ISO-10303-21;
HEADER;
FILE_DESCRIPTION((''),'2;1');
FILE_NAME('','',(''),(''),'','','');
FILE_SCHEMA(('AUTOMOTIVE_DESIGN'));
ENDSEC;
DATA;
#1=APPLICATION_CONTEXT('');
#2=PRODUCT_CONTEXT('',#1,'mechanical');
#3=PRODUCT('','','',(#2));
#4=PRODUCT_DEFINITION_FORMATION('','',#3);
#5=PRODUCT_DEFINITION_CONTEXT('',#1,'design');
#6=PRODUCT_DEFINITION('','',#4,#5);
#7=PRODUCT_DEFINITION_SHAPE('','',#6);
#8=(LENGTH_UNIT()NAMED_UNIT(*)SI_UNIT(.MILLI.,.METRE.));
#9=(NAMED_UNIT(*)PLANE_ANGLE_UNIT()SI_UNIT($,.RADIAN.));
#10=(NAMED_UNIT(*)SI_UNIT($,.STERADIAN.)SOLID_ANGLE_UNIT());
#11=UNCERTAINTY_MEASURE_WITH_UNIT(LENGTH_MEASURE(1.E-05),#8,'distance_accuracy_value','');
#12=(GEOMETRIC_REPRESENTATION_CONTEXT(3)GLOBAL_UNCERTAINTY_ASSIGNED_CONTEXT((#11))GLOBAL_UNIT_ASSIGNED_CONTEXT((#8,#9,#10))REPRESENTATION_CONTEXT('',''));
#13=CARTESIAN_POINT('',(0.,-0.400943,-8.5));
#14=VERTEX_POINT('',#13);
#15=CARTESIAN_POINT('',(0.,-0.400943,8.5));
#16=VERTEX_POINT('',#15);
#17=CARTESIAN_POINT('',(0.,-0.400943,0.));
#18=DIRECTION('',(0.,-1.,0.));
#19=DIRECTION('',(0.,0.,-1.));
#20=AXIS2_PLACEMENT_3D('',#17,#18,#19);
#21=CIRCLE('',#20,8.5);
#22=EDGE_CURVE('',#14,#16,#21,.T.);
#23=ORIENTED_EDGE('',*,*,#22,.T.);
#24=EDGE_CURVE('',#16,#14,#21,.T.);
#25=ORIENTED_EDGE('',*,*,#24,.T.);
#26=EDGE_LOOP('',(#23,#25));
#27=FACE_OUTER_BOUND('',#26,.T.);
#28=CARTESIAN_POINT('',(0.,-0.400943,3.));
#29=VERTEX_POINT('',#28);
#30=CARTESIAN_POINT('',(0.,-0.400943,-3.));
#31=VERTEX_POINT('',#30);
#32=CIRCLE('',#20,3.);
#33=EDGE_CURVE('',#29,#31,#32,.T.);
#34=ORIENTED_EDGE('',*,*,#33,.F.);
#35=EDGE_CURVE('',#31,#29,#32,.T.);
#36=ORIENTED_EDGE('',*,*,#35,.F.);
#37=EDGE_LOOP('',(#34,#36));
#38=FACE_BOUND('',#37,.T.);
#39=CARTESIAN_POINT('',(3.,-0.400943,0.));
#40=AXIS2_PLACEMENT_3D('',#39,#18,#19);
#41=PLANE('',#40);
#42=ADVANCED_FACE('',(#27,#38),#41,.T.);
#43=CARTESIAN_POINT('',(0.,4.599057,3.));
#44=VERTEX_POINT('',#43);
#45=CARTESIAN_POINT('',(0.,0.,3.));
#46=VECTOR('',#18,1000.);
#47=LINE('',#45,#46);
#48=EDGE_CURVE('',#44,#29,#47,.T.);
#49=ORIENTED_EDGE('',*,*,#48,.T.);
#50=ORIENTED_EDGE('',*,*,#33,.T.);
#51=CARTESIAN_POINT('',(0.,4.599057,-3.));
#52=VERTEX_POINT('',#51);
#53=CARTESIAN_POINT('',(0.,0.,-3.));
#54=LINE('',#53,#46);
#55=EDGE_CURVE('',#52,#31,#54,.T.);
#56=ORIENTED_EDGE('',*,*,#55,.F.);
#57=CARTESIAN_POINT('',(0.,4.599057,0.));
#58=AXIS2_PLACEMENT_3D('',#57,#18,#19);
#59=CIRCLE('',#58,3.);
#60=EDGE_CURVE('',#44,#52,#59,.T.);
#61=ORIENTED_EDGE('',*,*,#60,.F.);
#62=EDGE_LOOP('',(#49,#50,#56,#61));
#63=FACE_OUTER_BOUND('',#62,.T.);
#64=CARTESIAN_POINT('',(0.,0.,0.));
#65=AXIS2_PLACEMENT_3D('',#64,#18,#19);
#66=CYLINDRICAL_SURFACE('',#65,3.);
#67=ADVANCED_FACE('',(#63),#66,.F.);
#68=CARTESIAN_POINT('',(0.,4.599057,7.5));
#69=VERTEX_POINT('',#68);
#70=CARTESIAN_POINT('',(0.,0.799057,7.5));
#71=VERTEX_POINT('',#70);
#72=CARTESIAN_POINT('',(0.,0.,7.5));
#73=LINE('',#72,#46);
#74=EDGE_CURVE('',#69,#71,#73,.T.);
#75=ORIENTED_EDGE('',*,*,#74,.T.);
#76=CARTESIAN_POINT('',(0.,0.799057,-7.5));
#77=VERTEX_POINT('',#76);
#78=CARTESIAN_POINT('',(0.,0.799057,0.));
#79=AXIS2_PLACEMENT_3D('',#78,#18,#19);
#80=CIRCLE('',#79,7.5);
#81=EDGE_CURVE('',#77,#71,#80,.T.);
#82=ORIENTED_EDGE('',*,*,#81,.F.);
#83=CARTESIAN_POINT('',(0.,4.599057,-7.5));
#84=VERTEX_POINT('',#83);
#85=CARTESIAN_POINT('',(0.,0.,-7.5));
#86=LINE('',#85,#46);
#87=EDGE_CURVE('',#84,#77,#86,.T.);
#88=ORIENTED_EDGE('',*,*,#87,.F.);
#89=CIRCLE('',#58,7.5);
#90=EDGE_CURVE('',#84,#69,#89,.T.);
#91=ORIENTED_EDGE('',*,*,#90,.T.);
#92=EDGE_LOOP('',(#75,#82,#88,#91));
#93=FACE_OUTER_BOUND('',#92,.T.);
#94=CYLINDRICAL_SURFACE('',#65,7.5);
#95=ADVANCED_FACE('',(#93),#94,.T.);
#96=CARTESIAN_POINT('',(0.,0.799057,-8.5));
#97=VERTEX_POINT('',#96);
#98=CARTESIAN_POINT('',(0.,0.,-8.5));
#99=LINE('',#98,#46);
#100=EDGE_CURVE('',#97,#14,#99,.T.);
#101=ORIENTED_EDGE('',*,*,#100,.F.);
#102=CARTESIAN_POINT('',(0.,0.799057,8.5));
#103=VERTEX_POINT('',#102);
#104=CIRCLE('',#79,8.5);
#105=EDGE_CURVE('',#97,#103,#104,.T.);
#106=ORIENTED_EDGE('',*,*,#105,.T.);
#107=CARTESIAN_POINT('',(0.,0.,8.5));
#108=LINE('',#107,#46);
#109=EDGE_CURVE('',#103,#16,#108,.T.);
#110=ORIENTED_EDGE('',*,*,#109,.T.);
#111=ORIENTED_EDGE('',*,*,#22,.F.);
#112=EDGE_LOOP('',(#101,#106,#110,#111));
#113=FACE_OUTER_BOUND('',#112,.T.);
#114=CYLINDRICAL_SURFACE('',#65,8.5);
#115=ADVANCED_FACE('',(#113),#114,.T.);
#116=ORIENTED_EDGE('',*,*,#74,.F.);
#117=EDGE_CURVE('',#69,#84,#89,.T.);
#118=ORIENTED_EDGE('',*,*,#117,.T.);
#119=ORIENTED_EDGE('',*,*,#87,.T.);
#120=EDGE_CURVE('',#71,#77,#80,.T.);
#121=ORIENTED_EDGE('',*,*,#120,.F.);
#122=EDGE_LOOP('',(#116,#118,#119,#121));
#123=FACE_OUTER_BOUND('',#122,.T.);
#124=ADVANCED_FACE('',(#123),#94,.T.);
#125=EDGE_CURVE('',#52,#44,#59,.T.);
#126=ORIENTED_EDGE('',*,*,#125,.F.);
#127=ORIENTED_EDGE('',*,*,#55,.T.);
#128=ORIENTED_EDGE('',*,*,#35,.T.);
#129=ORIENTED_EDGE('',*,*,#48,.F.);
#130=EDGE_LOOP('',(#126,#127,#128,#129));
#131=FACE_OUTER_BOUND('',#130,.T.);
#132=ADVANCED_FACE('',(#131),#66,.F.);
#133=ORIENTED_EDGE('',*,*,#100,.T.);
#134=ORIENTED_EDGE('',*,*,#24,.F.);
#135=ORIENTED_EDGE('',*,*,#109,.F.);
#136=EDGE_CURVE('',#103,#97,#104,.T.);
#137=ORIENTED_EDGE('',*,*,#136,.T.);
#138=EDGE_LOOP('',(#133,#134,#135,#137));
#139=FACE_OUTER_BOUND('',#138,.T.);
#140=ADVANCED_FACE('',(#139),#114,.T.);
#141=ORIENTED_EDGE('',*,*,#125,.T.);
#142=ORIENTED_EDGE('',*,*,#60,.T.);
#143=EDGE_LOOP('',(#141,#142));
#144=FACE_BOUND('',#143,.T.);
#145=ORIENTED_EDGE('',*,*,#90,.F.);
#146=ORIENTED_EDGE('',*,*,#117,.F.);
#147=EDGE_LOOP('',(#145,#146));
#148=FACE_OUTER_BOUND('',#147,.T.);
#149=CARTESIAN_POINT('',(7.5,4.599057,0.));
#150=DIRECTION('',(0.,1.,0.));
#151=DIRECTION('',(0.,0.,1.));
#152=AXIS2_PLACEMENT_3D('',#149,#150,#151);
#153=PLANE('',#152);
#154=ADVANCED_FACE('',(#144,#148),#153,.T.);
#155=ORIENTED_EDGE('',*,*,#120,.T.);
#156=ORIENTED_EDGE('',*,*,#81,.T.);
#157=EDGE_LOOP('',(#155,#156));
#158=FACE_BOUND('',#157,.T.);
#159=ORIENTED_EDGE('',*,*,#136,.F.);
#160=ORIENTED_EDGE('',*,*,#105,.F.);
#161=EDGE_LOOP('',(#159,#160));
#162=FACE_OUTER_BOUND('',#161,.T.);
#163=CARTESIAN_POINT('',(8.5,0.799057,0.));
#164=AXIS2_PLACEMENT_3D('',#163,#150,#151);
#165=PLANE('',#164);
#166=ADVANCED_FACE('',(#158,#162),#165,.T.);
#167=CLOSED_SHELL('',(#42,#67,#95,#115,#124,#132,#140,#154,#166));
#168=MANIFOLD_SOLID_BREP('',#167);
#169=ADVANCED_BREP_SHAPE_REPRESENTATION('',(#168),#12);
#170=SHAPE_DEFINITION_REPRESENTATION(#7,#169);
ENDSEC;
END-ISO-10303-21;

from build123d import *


with BuildPart() as part:
    # 草图1 → 旋转1 (revolve)
    with BuildSketch(Plane.XY, mode=Mode.PRIVATE) as revolve_1_sk:
        Polygon((3, 4.599056604), (3, -0.400943396), (8.5, -0.400943396), (8.5, 0.799056604), (7.5, 0.799056604), (7.5, 4.599056604), align=None)
    revolve(revolve_1_sk.sketch.rotate(Axis((0, 0, 0), (0, 1, 0)), 90), axis=Axis((0, 0, 0), (0, 1, 0)))


solid = part.part
